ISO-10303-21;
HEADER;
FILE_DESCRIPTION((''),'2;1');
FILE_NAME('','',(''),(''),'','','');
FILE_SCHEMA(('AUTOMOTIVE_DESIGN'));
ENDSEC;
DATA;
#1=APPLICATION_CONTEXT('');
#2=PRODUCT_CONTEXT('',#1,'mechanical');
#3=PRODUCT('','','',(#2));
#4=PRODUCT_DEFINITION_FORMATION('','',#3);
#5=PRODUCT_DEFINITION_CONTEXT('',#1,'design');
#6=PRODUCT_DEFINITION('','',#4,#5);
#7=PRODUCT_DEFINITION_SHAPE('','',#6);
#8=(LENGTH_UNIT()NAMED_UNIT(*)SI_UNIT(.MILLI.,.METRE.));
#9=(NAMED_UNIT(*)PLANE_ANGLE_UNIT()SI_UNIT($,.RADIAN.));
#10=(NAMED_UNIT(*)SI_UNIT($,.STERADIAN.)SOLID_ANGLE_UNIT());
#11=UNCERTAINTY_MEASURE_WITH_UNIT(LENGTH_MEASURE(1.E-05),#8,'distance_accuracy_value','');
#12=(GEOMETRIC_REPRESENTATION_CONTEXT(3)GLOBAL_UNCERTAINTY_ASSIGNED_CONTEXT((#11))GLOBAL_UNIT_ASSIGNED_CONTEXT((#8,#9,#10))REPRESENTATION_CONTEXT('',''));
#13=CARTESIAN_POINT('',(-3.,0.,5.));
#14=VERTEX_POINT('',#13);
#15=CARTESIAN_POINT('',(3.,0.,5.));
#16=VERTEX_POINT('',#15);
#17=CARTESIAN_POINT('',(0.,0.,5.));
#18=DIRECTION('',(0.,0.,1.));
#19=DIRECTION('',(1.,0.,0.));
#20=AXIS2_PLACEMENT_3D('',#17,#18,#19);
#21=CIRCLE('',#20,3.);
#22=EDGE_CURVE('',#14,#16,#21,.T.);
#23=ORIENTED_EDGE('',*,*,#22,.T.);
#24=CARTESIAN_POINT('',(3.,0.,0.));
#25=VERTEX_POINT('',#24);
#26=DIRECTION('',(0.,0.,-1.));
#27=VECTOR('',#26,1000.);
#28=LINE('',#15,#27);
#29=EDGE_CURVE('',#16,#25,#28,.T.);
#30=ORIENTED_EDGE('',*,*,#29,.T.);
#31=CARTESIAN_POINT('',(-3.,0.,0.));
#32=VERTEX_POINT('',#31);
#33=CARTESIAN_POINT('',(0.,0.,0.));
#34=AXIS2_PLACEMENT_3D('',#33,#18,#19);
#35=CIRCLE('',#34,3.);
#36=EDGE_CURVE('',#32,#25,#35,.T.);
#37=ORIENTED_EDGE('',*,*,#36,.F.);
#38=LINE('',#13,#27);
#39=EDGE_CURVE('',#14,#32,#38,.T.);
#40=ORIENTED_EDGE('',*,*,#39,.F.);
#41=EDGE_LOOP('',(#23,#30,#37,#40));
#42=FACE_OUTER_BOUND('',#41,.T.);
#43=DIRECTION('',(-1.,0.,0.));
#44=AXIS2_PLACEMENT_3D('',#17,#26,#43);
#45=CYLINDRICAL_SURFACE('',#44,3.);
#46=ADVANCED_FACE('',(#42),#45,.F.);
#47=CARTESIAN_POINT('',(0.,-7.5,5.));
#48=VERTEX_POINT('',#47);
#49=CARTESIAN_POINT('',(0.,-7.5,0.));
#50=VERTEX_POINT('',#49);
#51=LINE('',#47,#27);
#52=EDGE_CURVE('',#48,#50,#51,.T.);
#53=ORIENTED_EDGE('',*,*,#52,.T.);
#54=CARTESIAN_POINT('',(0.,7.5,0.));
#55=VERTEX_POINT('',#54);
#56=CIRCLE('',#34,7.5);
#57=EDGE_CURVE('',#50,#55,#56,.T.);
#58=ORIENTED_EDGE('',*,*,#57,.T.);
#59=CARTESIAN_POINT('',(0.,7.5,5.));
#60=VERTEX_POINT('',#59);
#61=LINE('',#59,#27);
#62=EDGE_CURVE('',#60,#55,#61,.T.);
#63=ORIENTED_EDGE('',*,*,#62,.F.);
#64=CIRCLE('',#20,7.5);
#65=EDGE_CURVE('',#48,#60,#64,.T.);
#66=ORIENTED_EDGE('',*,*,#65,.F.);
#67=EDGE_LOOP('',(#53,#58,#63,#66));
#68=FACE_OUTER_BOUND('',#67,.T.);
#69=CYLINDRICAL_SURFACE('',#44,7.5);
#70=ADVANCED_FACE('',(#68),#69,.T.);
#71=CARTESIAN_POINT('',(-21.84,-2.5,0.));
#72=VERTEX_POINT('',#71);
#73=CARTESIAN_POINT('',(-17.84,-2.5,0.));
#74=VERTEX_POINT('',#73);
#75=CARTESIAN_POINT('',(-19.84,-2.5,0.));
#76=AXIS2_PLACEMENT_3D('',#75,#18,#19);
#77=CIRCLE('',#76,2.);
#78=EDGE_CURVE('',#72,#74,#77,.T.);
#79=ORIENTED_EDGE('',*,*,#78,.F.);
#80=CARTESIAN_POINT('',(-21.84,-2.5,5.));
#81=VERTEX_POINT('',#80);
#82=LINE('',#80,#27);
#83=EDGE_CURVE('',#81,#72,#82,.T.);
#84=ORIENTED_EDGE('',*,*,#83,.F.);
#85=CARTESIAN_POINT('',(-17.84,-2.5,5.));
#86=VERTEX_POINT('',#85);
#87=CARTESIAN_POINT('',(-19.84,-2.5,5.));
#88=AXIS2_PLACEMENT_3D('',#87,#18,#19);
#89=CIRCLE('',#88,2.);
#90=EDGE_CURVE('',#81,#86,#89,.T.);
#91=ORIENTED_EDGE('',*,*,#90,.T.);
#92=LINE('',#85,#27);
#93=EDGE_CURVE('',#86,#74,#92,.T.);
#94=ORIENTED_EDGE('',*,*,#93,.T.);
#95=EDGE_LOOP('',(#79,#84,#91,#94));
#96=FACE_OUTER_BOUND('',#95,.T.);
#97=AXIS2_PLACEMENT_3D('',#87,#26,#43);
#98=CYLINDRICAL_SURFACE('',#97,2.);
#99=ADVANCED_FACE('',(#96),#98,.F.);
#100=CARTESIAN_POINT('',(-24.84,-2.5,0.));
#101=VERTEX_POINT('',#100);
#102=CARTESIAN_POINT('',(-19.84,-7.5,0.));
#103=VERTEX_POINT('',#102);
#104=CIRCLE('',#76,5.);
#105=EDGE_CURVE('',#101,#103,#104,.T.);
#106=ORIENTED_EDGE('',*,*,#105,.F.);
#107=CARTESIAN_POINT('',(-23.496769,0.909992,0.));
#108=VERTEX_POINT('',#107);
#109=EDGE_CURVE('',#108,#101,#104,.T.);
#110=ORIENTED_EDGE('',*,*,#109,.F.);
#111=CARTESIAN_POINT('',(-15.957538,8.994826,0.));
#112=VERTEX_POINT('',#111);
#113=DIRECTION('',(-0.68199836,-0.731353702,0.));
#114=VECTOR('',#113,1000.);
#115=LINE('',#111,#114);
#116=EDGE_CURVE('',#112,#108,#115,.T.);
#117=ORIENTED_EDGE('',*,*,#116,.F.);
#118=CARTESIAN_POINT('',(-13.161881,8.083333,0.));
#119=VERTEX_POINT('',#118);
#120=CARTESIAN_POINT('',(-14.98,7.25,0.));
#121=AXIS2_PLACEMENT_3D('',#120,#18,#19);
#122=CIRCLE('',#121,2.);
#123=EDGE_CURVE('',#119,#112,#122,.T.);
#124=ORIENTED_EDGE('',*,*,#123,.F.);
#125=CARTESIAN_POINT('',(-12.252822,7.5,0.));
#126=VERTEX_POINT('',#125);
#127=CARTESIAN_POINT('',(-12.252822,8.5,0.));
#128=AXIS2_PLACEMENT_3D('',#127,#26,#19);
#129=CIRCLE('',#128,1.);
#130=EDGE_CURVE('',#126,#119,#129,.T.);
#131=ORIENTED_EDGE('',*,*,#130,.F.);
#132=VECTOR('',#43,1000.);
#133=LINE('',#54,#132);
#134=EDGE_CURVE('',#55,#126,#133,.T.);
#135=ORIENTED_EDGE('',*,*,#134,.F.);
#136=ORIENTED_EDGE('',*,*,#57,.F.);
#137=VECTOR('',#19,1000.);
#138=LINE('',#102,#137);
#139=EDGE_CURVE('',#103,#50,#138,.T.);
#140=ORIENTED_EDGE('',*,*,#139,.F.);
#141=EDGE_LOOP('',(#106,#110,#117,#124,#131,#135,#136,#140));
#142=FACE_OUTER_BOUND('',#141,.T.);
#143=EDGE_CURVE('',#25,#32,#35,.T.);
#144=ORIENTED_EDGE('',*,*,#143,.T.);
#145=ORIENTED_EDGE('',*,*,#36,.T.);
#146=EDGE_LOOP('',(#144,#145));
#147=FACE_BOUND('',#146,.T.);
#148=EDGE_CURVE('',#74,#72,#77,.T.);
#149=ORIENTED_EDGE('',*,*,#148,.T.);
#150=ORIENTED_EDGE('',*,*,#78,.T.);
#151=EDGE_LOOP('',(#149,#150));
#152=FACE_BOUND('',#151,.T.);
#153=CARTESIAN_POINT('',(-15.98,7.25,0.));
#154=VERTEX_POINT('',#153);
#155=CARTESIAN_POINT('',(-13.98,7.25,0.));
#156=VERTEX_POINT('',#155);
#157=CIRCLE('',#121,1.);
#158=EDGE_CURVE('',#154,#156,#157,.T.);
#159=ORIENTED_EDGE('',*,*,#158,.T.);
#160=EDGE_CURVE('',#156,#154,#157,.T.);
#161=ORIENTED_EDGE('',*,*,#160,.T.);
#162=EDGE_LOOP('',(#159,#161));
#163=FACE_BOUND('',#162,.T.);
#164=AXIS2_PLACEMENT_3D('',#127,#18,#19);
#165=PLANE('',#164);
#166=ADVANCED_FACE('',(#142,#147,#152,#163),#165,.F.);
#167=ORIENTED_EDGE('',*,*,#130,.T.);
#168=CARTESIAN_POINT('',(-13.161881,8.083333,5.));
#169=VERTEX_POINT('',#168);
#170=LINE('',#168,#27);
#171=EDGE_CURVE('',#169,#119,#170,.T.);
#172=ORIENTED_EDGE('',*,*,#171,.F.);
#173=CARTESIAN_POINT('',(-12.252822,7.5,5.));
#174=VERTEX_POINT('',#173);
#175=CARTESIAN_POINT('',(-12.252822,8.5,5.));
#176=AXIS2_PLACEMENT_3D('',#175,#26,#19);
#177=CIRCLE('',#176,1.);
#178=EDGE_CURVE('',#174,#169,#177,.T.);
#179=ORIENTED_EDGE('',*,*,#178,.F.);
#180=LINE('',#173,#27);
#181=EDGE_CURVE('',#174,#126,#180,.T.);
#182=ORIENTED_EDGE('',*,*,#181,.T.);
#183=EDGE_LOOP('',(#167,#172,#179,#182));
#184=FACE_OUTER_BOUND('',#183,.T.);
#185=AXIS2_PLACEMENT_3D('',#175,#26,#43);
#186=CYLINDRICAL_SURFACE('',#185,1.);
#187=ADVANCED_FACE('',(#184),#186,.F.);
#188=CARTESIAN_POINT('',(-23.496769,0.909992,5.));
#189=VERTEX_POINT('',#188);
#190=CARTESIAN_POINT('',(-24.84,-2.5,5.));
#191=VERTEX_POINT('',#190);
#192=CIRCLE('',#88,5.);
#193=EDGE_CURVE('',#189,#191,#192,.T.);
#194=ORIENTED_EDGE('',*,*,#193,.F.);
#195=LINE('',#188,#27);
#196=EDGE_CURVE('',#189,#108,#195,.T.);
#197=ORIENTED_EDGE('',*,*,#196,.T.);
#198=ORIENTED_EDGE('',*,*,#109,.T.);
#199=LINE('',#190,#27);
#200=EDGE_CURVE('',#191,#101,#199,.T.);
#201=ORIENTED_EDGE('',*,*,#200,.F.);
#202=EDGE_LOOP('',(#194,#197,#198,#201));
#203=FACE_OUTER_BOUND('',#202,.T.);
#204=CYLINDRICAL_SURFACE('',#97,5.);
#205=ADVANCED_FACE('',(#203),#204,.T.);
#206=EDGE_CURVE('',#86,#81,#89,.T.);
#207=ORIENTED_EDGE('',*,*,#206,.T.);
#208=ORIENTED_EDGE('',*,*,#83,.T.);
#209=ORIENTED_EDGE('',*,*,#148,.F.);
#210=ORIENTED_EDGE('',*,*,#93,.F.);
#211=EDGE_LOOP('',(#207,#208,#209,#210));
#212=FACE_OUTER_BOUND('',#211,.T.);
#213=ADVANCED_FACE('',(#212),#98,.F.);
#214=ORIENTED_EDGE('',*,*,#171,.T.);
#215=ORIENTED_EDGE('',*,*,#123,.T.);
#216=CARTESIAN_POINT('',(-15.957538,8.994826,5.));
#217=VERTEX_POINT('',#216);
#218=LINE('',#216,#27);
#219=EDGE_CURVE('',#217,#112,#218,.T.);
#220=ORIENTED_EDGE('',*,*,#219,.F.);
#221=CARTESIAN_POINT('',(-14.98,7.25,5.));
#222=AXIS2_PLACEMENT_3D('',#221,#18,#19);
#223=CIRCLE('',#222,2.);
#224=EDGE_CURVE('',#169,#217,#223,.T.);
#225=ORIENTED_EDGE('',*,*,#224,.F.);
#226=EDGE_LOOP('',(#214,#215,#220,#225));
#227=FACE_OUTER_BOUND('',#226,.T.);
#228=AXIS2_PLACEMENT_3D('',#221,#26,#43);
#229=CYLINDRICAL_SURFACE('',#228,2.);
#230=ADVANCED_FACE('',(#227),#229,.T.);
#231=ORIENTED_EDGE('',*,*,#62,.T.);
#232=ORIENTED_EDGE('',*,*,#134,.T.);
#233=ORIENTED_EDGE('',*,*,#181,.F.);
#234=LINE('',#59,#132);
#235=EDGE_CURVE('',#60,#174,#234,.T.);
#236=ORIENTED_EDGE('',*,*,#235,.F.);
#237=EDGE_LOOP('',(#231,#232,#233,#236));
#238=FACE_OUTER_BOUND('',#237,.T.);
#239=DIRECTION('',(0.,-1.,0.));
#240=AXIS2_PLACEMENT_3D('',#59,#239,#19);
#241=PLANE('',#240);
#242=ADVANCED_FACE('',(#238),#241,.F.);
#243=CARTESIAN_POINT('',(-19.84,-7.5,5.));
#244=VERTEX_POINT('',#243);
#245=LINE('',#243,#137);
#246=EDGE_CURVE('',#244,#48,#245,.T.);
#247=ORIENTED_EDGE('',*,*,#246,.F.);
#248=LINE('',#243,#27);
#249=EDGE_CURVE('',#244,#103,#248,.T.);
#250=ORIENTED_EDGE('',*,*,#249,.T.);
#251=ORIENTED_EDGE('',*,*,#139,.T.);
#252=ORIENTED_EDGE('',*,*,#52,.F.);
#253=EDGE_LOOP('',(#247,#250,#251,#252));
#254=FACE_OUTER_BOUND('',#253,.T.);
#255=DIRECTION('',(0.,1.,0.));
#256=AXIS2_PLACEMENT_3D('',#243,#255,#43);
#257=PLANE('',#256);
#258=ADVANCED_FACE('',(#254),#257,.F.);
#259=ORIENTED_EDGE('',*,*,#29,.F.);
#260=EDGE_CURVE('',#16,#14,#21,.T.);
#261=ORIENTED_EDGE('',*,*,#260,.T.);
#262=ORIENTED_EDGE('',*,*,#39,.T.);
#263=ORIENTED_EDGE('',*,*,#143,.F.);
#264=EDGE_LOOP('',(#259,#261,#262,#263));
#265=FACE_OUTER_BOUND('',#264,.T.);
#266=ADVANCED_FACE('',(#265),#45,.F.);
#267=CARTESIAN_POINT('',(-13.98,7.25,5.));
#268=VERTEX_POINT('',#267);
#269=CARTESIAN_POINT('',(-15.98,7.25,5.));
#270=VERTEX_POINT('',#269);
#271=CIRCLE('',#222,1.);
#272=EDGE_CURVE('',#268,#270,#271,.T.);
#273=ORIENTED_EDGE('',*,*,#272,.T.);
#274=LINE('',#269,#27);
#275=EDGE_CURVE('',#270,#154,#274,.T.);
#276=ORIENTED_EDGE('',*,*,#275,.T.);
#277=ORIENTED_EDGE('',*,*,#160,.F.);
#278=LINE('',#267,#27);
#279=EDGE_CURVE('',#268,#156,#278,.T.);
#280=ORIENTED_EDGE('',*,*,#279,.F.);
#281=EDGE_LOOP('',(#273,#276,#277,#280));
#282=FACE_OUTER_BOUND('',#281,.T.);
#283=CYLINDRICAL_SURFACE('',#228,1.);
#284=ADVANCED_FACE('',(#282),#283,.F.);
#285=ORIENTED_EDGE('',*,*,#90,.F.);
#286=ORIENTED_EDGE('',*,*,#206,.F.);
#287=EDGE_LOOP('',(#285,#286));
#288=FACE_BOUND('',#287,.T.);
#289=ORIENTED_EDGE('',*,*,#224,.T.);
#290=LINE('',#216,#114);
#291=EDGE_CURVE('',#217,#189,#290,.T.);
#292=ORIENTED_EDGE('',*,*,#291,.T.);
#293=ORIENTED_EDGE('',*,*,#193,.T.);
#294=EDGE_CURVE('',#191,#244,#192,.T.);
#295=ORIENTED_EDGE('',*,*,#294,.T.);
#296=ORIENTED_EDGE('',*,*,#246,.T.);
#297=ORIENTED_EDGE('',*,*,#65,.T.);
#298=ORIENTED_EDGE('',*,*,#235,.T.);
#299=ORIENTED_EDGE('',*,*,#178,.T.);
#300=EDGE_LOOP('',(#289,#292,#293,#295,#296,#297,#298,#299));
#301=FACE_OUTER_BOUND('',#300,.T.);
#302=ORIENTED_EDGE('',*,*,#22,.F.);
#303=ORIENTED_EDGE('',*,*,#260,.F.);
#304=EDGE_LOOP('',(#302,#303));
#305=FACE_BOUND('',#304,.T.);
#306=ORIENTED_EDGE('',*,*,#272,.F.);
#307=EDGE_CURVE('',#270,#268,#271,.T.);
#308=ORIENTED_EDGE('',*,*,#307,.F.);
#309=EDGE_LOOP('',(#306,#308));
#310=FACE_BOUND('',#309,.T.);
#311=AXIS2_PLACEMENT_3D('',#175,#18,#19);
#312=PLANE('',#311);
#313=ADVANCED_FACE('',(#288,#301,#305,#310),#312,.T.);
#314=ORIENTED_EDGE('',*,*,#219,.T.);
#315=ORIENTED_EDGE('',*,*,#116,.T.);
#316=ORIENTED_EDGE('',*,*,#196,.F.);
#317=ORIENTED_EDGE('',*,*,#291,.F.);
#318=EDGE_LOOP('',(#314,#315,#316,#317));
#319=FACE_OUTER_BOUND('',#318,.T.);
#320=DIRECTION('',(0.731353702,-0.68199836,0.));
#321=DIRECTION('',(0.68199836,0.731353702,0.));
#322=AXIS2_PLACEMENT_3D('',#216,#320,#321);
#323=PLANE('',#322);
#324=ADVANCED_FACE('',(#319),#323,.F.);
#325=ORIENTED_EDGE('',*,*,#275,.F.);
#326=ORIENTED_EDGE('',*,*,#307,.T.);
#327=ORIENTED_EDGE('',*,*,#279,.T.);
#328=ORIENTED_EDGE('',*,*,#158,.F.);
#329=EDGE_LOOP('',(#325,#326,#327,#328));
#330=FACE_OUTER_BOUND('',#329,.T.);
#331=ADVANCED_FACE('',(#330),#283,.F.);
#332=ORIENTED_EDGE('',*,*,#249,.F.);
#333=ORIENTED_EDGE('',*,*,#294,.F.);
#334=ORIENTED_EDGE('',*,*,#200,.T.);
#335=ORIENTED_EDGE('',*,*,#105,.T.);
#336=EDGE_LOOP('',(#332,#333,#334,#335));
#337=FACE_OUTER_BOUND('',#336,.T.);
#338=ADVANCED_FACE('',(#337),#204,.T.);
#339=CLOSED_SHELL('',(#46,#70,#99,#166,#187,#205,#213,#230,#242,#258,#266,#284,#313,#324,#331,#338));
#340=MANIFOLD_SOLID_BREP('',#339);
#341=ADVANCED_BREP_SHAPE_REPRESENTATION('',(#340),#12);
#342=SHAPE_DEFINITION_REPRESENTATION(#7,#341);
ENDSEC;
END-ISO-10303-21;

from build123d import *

# Parameters (mm, degrees)
SKETCH1_R           = 3
SKETCH1_R_2         = 1
SKETCH1_R_3         = 2
BOSS_EXTRUDE1_DEPTH = 5


with BuildPart() as part:
    # Sketch1 → Boss-Extrude1 (new body)
    with BuildSketch(Plane.XY):
        with BuildLine():
            Line((-19.84, -7.5), (0, -7.5))
            ThreePointArc((0, -7.5), (7.5, 0), (0, 7.5))
            Line((0, 7.5), (-12.252821971, 7.5))
            ThreePointArc((-12.252821971, 7.5), (-12.792883696, 7.658374588), (-13.161881314, 8.083333333))
            ThreePointArc((-13.161881314, 8.083333333), (-14.360041425, 9.15148662), (-15.957538412, 8.994826253))
            Line((-15.957538412, 8.994826253), (-23.496768508, 0.9099918))
            ThreePointArc((-23.496768508, 0.9099918), (-24.425300372, -4.493745345), (-19.84, -7.5))
        make_face()
        Circle(SKETCH1_R, mode=Mode.SUBTRACT)
        with Locations((-14.98, 7.25)):
            Circle(SKETCH1_R_2, mode=Mode.SUBTRACT)
        with Locations((-19.84, -2.5)):
            Circle(SKETCH1_R_3, mode=Mode.SUBTRACT)
    extrude(amount=BOSS_EXTRUDE1_DEPTH)


solid = part.part
